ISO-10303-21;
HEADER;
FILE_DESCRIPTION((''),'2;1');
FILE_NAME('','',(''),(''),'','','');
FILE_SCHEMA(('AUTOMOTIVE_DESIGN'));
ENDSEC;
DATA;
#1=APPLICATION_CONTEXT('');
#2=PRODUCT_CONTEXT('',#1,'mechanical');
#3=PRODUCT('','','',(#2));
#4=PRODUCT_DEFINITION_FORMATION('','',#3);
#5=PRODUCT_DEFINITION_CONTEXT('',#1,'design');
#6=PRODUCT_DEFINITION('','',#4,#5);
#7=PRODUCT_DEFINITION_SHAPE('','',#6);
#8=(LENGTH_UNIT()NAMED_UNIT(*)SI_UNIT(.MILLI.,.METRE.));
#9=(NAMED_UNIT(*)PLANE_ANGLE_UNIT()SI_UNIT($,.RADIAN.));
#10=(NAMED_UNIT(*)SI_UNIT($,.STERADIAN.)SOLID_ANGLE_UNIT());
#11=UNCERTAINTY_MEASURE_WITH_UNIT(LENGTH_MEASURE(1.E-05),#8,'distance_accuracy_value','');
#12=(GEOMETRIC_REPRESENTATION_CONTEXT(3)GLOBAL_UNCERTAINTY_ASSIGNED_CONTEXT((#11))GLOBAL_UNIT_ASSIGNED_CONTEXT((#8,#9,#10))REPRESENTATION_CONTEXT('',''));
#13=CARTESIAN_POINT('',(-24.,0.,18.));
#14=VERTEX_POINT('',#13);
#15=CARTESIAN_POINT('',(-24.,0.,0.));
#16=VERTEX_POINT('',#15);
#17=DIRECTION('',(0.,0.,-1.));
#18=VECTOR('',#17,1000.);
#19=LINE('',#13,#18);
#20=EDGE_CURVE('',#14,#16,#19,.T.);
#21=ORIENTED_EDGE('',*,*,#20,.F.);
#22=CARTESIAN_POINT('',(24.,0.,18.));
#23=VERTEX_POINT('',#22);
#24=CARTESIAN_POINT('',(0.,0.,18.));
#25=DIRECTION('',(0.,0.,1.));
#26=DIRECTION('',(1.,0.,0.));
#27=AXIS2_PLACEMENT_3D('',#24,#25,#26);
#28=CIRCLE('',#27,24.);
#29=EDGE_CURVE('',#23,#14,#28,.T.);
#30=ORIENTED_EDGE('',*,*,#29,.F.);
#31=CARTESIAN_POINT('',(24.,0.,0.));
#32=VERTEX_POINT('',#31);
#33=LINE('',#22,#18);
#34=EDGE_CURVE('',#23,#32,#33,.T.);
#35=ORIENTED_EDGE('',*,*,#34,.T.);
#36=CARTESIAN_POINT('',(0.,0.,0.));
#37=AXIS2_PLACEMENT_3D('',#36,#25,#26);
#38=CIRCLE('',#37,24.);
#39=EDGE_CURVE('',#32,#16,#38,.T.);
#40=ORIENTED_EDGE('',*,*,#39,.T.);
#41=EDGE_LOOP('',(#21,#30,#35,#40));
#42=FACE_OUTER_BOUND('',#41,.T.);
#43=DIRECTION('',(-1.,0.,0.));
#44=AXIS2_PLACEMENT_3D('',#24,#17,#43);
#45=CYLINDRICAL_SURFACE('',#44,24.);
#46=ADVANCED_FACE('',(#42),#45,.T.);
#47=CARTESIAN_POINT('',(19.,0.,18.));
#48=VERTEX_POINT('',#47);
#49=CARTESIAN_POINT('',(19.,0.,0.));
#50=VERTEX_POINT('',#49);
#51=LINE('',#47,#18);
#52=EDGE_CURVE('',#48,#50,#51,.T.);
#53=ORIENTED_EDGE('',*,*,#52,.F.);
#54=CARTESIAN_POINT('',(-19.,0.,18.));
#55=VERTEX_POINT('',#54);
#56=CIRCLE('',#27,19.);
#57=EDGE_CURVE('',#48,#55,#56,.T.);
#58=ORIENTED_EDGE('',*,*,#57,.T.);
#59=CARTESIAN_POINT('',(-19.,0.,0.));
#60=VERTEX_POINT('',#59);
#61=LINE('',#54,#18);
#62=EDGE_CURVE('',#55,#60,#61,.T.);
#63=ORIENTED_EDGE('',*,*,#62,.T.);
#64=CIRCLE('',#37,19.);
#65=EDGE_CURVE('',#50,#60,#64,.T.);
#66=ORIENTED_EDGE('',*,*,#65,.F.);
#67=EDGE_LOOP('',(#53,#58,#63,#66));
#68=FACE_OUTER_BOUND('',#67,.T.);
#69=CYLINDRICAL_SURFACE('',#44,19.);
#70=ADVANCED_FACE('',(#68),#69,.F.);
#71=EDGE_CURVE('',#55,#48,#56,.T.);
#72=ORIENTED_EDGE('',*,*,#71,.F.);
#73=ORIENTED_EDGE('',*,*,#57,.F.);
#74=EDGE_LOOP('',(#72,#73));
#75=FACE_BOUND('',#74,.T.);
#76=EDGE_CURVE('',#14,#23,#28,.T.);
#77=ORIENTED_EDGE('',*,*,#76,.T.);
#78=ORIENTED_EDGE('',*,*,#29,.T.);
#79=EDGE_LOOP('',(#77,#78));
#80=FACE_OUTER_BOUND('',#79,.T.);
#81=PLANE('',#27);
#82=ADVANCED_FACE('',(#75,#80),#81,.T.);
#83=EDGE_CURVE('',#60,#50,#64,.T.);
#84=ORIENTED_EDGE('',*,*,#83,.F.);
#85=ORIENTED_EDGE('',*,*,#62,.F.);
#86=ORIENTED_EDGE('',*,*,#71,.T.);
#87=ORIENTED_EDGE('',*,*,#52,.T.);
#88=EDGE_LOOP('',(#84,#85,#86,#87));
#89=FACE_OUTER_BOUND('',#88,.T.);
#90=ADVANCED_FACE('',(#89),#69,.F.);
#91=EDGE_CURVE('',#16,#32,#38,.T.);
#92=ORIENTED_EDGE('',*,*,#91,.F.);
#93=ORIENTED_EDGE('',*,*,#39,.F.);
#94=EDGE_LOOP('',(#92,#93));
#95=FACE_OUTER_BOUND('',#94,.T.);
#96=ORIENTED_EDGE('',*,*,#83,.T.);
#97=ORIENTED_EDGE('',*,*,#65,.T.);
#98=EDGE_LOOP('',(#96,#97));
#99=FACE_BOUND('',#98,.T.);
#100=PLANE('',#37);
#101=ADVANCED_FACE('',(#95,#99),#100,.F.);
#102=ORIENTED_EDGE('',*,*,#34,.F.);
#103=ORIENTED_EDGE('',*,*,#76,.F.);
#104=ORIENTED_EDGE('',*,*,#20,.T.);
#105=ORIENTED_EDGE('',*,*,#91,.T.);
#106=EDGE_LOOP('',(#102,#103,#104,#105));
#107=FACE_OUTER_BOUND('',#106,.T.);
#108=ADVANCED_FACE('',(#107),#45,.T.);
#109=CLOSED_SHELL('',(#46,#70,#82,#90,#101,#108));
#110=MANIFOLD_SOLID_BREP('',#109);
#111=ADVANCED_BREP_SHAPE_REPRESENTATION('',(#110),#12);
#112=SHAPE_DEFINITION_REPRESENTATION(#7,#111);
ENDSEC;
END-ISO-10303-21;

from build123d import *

# Parameters (mm, degrees)
SKETCH_1_R      = 24
SKETCH_1_R_2    = 19
EXTRUDE_1_DEPTH = 18


with BuildPart() as part:
    # 草图1 → 凸台-拉伸1 (new body)
    with BuildSketch(Plane.XY):
        Circle(SKETCH_1_R)
        Circle(SKETCH_1_R_2, mode=Mode.SUBTRACT)
    extrude(amount=EXTRUDE_1_DEPTH)


solid = part.part
